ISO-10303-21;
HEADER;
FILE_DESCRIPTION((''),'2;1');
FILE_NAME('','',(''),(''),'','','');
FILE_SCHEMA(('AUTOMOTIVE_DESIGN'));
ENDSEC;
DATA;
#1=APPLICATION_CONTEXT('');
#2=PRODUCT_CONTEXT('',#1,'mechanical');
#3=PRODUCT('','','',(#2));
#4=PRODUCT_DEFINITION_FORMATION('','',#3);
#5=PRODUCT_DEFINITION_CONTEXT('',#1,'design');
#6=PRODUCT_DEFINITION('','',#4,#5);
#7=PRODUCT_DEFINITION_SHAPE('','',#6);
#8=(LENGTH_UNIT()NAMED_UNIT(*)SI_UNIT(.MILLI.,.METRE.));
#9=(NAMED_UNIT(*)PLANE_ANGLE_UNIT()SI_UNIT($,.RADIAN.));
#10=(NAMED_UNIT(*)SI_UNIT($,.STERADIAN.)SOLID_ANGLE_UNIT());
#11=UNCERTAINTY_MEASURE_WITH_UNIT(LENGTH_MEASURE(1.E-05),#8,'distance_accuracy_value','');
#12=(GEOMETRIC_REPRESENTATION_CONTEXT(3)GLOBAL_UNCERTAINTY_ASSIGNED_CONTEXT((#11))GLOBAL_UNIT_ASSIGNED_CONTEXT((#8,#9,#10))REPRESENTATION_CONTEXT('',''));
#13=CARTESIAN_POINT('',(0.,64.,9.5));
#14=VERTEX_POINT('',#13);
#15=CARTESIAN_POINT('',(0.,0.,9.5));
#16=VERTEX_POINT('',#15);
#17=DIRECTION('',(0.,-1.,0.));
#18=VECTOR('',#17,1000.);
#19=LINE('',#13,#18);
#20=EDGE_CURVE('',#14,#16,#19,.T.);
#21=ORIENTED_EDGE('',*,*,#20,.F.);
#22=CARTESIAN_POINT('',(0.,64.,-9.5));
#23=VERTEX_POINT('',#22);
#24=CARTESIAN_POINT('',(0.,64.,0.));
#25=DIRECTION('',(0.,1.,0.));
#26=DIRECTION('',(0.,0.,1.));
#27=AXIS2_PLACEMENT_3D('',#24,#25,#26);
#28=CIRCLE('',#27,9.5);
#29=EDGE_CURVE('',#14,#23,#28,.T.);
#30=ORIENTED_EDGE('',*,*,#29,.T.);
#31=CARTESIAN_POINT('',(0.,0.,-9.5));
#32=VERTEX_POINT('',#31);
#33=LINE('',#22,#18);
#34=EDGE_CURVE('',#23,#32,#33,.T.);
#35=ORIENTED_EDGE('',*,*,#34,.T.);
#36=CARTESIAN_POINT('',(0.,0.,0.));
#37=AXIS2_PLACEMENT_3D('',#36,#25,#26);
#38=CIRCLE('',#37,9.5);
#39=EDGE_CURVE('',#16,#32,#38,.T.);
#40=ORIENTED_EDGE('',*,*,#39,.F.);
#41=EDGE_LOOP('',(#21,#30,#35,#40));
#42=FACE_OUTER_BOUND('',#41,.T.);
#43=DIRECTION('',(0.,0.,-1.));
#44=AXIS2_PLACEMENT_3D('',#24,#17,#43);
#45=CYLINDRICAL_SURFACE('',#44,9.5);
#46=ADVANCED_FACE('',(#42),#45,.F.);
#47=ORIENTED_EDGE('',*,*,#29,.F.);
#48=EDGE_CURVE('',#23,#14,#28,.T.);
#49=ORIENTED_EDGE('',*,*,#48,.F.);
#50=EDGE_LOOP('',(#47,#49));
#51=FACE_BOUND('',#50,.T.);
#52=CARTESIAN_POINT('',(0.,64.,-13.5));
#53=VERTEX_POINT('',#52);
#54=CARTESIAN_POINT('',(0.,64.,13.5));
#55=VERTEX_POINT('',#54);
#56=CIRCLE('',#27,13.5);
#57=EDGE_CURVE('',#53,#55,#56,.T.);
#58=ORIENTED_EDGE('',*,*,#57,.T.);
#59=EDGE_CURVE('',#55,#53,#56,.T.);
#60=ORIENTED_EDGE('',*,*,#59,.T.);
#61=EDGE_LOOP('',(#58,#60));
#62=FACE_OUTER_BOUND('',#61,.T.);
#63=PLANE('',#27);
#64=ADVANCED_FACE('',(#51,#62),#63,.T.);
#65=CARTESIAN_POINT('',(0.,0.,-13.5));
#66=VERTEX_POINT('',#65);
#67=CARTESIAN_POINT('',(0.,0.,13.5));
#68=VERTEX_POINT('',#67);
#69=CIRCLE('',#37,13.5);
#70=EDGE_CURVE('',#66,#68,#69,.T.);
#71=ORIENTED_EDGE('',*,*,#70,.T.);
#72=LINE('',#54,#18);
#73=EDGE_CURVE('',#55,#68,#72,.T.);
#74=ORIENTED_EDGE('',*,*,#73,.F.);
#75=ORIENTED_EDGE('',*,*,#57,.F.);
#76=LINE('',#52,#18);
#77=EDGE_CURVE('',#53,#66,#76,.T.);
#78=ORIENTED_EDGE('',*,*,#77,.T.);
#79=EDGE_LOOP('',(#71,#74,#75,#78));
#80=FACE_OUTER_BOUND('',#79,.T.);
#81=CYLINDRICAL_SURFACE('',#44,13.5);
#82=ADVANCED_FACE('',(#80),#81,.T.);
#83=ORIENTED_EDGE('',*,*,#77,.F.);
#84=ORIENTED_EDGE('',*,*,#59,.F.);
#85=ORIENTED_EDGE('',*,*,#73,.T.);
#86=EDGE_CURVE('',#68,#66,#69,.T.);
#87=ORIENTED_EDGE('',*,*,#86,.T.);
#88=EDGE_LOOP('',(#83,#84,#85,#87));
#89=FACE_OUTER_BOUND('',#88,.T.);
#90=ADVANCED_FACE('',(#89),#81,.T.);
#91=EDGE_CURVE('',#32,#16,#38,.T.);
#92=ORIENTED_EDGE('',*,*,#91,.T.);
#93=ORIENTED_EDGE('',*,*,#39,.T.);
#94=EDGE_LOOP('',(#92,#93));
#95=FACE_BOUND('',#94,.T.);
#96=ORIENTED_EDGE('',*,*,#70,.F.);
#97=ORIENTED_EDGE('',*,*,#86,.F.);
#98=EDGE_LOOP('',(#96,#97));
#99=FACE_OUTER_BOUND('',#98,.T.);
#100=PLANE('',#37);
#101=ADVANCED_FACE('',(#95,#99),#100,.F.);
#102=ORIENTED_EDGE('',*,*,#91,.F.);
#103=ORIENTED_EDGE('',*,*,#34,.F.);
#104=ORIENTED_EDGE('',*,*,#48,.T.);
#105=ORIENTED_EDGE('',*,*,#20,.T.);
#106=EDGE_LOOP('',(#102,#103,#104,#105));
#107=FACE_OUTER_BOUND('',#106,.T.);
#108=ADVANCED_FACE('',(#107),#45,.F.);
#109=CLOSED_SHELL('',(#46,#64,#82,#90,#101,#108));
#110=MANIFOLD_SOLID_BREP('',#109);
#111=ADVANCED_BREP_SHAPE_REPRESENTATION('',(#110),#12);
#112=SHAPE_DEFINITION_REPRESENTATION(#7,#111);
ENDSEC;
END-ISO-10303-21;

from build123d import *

# Parameters (mm, degrees)
SKETCH1_R      = 13.5
SKETCH1_R_2    = 9.5
EXTRUDE1_DEPTH = 64


with BuildPart() as part:
    # Sketch1 → Extrude1 (new body)
    with BuildSketch(Plane(origin=(0, 0, 0), x_dir=(1, 0, 0), z_dir=(0, 1, 0))):
        with Locations(Location((0, 0, 0), (0, 0, 270))):
            Circle(SKETCH1_R)
        with Locations(Location((0, 0, 0), (0, 0, 270))):
            Circle(SKETCH1_R_2, mode=Mode.SUBTRACT)
    extrude(amount=EXTRUDE1_DEPTH)


solid = part.part
